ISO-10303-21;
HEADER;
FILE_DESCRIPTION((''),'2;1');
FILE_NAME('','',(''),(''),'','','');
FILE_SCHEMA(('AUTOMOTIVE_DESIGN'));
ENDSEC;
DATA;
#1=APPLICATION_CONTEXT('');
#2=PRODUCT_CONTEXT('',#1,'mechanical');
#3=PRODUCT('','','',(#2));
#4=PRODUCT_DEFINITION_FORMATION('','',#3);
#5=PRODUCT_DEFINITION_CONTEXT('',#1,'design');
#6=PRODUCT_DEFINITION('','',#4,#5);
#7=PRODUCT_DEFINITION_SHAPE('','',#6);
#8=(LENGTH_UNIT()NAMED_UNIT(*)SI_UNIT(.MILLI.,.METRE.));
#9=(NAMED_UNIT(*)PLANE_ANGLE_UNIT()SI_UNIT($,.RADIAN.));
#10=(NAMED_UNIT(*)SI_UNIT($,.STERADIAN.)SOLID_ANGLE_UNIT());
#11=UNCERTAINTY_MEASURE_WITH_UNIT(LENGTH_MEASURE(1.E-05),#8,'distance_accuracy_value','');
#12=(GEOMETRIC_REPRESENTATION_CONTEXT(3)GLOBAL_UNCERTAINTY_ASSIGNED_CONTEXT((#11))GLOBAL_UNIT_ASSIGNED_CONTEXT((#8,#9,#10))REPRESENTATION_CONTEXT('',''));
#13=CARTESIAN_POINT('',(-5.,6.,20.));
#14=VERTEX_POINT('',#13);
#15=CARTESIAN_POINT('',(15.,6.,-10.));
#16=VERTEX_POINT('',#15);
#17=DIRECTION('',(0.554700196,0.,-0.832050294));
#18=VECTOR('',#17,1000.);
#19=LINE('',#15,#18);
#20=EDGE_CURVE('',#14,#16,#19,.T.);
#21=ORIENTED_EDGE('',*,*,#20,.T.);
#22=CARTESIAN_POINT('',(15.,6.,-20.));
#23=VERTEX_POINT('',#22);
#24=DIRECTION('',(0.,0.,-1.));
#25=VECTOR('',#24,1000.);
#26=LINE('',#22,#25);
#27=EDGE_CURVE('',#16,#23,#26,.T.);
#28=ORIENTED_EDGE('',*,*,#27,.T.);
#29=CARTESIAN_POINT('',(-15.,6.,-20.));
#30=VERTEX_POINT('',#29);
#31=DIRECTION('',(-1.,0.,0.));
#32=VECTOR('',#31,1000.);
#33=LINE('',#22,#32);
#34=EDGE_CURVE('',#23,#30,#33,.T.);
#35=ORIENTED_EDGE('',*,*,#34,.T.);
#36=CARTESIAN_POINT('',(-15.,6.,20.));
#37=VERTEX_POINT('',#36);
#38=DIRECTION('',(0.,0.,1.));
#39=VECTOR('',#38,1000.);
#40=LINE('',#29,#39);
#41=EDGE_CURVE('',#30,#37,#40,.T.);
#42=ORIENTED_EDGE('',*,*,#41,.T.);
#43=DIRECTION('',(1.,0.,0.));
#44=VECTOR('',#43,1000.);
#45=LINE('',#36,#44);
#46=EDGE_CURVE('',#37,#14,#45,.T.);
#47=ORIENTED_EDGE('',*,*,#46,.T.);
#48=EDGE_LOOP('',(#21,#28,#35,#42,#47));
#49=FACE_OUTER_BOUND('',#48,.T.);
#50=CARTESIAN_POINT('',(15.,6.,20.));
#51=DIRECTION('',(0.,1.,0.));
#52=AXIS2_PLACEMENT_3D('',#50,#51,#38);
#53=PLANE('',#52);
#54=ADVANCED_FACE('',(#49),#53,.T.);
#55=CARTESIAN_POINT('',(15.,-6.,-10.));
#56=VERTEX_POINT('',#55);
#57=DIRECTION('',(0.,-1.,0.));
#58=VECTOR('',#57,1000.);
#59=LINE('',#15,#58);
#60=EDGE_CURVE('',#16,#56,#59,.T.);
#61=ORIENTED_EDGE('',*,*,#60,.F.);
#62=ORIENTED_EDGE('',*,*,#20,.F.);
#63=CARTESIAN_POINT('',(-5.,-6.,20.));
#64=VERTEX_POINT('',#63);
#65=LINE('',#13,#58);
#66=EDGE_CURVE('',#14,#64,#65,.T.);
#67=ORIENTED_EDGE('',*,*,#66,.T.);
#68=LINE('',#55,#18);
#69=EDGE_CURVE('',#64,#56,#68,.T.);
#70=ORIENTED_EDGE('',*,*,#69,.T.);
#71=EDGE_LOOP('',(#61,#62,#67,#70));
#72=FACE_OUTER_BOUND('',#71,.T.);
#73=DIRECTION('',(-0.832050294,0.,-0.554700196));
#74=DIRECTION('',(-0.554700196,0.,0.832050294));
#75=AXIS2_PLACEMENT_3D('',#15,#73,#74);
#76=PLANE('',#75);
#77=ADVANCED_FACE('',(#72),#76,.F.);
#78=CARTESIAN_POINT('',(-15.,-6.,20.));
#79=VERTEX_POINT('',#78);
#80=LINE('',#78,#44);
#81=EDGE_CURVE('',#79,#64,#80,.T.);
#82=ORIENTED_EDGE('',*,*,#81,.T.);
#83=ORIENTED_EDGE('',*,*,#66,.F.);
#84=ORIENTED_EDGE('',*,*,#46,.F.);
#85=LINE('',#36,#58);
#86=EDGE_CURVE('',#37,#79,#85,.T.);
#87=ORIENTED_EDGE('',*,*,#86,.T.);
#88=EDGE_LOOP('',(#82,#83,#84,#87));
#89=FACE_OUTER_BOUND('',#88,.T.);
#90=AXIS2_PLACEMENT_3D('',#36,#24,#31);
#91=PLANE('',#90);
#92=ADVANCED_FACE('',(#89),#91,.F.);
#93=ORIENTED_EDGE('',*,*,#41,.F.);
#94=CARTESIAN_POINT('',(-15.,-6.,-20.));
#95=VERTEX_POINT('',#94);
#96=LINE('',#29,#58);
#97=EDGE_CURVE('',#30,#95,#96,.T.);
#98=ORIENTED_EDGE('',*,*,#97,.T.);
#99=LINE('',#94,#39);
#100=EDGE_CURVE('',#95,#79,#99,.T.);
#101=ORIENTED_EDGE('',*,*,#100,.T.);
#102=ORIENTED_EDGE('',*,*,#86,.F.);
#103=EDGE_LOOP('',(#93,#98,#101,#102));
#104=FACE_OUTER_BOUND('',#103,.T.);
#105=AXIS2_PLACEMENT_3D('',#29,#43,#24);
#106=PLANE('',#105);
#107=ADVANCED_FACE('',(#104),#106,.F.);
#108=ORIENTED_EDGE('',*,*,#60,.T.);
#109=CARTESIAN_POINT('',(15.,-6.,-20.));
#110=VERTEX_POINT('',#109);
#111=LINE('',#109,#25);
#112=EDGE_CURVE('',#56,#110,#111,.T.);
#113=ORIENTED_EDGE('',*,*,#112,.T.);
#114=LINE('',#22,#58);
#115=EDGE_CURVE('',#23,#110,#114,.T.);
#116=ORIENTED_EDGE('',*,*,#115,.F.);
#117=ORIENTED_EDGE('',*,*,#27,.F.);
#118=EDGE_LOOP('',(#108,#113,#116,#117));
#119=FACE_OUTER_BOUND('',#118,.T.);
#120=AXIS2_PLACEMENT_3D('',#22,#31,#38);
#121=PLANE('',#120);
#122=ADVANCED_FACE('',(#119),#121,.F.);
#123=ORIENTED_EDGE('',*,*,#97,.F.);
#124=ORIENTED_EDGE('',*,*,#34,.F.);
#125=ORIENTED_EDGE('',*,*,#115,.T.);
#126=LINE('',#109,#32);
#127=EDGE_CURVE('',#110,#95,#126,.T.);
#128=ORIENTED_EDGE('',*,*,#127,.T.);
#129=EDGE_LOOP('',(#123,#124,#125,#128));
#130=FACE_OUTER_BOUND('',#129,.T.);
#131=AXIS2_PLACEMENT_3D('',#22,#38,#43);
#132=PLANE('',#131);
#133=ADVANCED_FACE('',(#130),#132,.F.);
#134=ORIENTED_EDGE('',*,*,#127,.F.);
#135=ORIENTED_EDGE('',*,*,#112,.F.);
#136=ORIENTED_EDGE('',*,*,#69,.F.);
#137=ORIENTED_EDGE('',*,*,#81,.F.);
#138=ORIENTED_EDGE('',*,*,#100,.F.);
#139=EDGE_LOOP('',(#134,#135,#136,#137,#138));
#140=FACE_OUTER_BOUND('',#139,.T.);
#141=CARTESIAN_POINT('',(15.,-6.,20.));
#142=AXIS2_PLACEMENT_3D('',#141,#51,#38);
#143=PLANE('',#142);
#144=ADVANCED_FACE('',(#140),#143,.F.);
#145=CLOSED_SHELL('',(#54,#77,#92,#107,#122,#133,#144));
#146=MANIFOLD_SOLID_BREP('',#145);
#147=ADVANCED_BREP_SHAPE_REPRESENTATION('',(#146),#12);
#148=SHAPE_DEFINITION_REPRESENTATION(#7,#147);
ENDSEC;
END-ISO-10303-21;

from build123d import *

# Parameters (mm, degrees)
EXTRUDE1_DEPTH = 6


with BuildPart() as part:
    # Sketch1 → Extrude1 (new, symmetric)
    with BuildSketch(Plane(origin=(0, 0, 0), x_dir=(1, 0, 0), z_dir=(0, 1, 0))):
        Polygon((-15, -20), (-5, -20), (15, 10), (15, 20), (-15, 20), align=None)
    extrude(amount=EXTRUDE1_DEPTH, both=True)


solid = part.part
